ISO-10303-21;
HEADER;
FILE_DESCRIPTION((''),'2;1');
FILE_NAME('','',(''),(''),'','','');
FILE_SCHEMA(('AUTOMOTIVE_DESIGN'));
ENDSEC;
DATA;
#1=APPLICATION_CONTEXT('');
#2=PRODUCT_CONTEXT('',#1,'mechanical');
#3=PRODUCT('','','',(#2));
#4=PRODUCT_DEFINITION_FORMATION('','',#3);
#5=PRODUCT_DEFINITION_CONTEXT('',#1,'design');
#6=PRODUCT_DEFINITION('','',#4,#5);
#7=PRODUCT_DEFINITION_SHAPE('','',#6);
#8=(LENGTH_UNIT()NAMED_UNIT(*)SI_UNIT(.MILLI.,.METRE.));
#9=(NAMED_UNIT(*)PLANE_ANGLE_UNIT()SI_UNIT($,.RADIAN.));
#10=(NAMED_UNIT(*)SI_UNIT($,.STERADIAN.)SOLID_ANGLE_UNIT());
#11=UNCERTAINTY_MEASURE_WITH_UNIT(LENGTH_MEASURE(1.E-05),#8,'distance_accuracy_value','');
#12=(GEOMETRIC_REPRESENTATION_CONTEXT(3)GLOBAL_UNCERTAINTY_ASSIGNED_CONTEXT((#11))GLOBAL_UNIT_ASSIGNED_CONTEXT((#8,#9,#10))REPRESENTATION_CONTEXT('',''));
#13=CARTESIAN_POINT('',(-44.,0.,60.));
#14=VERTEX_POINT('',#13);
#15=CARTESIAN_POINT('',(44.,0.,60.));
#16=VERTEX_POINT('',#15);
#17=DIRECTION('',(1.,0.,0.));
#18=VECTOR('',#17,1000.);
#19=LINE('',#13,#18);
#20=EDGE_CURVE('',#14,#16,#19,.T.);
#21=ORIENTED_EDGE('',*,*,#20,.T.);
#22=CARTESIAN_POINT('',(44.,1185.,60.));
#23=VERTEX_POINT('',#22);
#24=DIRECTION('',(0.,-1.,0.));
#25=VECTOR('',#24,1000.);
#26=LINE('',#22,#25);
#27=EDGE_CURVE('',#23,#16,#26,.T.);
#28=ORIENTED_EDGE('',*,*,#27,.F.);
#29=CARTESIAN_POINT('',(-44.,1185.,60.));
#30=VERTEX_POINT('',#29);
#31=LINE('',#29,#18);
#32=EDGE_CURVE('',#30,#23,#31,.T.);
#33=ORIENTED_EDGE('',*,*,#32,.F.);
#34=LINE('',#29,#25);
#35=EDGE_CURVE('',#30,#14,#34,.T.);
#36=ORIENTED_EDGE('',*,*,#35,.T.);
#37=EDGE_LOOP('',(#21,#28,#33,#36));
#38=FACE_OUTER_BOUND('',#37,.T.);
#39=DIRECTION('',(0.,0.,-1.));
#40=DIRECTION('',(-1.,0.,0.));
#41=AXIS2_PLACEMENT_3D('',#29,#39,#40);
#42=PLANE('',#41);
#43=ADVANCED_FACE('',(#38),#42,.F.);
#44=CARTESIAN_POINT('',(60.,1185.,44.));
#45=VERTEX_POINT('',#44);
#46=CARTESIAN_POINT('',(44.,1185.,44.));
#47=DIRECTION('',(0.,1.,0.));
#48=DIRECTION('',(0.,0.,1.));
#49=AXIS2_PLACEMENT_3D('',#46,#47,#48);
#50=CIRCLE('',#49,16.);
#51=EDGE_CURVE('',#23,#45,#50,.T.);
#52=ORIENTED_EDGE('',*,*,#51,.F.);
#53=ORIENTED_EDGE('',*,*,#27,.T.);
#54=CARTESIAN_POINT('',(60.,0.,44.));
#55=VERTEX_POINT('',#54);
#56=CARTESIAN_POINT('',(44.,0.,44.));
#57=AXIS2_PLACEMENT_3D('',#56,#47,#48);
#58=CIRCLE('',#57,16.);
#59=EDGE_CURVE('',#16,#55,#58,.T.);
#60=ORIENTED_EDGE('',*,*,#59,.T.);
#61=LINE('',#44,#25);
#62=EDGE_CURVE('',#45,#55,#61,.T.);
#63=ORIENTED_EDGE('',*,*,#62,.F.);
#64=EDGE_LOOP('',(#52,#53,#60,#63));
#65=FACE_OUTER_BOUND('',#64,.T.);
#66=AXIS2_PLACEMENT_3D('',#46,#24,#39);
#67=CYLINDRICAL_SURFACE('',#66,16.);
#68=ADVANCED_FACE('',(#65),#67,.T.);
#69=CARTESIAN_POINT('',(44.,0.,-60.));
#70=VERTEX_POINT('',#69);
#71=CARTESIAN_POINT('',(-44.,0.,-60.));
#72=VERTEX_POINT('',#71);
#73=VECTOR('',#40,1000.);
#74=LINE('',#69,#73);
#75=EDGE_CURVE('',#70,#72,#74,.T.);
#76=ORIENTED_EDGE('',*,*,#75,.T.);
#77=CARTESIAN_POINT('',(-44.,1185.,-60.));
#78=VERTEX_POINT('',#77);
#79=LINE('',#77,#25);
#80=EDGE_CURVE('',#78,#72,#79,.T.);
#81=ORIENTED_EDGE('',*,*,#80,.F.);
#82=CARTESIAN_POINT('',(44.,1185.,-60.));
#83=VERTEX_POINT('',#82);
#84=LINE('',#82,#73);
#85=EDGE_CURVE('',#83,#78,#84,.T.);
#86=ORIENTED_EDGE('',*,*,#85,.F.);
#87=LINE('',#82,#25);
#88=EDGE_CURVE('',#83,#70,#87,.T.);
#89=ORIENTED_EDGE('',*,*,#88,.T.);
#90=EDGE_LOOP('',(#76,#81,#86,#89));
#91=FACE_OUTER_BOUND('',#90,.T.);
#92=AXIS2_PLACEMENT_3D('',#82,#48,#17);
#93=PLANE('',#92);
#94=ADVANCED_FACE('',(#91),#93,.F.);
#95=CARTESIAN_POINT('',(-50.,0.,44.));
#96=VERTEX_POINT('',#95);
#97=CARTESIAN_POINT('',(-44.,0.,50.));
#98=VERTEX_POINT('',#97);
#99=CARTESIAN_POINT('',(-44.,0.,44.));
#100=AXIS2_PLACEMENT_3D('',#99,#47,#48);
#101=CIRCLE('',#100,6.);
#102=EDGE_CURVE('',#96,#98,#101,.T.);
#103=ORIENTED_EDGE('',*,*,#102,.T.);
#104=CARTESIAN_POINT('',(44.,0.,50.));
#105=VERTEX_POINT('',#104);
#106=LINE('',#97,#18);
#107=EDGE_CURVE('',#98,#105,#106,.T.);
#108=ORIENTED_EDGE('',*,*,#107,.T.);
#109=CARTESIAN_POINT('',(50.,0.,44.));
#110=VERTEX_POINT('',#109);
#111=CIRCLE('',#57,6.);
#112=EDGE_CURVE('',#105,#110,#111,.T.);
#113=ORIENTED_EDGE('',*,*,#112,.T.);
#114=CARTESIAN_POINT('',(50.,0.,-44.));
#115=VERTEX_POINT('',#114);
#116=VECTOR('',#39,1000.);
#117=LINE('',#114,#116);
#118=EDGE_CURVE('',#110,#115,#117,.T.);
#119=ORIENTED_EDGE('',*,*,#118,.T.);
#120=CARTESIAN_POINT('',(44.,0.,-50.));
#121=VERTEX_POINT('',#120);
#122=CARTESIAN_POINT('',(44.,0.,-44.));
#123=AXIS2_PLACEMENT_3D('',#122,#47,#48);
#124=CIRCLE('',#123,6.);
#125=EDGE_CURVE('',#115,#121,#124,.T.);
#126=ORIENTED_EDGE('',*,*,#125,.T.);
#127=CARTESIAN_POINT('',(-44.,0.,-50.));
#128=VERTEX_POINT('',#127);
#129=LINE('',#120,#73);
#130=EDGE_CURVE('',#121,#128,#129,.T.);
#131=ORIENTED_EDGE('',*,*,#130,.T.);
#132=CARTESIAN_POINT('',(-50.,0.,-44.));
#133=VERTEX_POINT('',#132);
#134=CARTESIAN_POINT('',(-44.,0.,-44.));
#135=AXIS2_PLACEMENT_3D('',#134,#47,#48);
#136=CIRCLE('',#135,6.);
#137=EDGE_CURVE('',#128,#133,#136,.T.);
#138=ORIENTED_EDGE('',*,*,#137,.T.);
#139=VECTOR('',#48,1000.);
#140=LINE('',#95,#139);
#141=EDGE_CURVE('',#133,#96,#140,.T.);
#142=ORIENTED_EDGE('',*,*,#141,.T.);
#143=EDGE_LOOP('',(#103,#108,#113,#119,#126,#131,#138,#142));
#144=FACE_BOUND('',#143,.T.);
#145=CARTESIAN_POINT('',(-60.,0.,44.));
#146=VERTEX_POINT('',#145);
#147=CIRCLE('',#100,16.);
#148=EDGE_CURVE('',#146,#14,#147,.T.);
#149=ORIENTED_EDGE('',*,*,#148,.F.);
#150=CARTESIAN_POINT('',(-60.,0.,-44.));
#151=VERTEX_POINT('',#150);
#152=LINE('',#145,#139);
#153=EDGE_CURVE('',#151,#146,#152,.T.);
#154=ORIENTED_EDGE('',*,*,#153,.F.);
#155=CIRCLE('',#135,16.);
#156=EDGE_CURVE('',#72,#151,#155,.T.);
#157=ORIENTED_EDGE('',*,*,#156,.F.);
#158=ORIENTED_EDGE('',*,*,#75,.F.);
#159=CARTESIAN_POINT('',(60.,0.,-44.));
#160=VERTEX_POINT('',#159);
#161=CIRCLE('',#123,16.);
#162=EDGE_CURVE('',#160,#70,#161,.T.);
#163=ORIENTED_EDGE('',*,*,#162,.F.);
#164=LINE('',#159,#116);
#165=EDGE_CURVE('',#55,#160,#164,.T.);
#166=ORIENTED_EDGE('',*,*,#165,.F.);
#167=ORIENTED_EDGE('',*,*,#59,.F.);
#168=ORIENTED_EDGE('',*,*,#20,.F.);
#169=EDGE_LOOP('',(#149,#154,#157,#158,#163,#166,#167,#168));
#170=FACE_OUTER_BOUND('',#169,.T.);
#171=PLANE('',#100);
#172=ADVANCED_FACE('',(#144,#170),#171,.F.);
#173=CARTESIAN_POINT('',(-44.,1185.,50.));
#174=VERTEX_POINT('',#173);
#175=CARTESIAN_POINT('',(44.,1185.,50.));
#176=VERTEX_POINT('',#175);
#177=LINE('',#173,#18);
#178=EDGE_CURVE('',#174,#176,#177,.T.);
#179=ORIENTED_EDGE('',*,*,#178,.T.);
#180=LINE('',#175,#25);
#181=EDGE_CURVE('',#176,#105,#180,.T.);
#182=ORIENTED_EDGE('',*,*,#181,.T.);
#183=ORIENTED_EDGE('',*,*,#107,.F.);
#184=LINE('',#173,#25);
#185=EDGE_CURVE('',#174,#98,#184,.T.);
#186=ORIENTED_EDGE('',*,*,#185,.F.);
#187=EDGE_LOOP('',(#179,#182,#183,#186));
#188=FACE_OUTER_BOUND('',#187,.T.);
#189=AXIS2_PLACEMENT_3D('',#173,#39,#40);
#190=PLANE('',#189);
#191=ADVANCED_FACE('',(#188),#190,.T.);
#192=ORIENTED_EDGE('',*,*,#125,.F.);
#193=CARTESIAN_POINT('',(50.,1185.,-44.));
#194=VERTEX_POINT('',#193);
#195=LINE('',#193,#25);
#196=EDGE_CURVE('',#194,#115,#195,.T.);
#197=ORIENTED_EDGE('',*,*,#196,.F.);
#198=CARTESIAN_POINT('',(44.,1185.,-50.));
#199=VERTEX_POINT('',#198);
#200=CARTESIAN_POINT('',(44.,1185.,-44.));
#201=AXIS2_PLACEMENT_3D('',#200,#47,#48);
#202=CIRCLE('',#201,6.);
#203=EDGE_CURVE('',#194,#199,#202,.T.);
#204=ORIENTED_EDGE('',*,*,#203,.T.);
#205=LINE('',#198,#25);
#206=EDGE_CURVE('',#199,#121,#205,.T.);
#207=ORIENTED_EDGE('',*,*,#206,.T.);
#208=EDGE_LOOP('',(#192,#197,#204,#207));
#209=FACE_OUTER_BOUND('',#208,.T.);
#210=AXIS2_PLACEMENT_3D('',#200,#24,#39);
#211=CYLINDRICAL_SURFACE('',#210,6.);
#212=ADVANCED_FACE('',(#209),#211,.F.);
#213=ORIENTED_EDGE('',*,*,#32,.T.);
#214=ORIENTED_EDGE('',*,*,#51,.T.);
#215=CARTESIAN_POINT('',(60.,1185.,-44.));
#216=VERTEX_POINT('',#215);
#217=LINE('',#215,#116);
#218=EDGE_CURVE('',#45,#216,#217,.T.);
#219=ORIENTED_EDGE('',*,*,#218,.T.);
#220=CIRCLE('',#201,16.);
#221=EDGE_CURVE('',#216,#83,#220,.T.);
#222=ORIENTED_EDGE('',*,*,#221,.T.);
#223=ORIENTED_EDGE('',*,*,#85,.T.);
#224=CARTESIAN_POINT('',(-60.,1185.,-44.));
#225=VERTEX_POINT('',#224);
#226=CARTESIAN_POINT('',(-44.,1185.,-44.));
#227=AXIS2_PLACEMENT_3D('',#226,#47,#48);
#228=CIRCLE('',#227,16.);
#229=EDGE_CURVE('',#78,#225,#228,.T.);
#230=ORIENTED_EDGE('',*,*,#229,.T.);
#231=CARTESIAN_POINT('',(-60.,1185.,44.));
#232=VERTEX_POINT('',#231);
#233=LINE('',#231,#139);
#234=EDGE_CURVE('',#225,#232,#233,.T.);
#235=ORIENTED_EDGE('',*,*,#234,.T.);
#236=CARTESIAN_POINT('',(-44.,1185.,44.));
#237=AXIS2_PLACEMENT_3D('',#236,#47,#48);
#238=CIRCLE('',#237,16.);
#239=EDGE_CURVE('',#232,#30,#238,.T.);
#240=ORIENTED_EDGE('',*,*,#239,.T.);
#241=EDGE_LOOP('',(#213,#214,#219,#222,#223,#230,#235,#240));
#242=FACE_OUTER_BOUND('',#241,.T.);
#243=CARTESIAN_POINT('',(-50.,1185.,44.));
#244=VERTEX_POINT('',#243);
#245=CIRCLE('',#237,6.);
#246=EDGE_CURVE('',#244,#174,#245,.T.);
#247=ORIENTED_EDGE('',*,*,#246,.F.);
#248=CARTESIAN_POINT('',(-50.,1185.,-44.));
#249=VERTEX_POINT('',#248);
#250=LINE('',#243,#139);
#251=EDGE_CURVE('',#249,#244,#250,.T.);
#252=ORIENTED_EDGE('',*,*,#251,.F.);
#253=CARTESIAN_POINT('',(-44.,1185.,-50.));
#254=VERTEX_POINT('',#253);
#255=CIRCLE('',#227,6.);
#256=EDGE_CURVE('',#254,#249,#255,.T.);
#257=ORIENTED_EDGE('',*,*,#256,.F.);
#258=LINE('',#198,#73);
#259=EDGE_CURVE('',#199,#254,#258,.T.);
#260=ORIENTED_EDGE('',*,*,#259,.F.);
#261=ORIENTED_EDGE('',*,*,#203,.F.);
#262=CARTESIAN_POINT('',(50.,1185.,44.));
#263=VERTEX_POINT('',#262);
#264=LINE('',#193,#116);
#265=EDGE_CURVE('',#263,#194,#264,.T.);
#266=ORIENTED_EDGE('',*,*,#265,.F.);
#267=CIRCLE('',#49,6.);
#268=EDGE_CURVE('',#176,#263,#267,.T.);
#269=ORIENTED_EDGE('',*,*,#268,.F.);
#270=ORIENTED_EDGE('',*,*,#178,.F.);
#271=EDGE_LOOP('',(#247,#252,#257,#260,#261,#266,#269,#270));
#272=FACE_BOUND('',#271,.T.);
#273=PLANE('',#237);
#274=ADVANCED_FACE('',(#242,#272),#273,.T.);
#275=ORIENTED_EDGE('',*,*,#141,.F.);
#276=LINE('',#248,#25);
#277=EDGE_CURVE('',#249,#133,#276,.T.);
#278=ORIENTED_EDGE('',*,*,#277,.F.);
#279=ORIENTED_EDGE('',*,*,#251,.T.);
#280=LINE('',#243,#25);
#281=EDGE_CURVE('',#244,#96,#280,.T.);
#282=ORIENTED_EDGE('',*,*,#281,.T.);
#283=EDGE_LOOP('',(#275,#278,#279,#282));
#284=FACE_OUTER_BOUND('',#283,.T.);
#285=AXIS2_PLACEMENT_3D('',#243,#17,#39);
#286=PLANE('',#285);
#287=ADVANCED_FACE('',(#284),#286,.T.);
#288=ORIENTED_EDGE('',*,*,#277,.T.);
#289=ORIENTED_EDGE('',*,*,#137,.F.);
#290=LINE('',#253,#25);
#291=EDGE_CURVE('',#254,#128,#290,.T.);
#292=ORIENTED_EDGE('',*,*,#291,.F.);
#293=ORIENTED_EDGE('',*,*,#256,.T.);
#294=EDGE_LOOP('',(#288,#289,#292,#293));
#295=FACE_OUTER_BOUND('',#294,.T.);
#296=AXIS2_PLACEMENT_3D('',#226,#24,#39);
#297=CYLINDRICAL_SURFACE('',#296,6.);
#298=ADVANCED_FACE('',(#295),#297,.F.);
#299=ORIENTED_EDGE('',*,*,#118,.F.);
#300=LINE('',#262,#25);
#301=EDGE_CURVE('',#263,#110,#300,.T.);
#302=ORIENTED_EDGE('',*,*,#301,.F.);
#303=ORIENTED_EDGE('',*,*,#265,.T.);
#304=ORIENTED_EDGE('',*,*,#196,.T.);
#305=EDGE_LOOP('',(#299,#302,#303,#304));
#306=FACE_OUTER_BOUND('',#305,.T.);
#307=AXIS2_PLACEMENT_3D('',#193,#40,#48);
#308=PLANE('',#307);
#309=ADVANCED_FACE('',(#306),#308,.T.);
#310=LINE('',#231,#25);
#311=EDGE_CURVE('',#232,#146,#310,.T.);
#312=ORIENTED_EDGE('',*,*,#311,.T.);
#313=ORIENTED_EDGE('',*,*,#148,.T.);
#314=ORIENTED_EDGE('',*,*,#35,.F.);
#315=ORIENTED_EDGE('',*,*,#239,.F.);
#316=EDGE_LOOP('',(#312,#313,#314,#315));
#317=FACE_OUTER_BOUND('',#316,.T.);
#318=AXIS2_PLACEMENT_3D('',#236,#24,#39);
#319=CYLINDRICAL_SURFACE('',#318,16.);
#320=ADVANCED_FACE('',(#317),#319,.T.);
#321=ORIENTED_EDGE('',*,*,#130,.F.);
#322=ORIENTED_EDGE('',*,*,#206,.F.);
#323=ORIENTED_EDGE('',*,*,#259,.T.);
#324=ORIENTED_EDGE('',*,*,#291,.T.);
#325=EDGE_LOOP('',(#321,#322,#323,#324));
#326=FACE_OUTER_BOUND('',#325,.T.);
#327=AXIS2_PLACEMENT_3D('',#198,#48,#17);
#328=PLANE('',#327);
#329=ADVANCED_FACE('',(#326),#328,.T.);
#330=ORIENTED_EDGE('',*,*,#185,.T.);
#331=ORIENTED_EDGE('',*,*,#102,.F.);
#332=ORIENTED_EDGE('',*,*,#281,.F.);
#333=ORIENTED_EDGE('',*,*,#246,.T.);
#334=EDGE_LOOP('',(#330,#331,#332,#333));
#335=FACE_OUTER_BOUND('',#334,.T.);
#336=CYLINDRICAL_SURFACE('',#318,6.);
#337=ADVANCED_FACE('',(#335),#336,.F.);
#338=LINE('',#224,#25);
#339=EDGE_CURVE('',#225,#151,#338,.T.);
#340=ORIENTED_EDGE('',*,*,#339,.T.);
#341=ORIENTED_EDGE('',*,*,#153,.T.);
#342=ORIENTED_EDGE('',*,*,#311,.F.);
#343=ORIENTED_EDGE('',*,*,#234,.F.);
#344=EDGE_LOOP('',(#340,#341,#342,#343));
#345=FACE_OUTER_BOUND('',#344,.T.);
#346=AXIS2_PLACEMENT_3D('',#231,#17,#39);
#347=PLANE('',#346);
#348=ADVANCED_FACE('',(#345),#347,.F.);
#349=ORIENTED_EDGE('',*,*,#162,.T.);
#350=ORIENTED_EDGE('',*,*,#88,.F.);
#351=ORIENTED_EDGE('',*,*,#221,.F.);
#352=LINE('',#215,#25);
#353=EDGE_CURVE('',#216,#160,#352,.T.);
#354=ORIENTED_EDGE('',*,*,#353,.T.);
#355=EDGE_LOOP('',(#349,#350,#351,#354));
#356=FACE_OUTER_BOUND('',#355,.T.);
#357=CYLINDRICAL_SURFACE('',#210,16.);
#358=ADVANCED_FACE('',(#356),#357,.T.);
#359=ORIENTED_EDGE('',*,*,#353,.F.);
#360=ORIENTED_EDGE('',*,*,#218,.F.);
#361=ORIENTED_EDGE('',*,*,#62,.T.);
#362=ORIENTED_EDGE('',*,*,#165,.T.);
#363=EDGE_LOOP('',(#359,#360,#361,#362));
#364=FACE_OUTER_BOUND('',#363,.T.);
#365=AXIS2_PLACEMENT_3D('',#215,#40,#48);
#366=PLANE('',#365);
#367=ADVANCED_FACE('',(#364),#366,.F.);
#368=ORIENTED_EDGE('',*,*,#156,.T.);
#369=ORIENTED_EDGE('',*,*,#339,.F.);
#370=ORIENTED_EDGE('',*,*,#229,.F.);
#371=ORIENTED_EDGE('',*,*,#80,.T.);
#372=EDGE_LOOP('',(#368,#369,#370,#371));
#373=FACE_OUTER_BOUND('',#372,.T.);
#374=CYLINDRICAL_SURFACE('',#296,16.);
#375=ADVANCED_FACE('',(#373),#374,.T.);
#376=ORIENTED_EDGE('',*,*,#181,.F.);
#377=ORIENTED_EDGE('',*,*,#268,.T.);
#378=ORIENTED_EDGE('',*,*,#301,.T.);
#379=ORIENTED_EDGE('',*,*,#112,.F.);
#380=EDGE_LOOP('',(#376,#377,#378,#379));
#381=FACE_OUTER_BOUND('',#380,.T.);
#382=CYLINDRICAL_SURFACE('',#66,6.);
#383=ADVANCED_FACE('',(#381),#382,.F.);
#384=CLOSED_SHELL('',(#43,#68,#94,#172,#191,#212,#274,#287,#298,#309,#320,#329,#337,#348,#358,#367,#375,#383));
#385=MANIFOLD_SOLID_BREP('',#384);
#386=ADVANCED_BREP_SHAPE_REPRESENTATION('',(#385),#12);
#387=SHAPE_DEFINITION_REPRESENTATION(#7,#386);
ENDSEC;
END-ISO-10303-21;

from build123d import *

# Parameters (mm, degrees)
GB_T6728_2002_120_120_10_1_DEPTH = 1185


with BuildPart() as part:
    # Sketch12 → 结构用冷弯空心方钢(gb t6728-2002) 120×120×10(1) (new body)
    with BuildSketch(Plane(origin=(0, 0, 0), x_dir=(-1, 0, 0), z_dir=(0, 1, 0))):
        with BuildLine():
            Line((-44, -60), (44, -60))
            ThreePointArc((44, -60), (55.313708499, -55.313708499), (60, -44))
            Line((60, -44), (60, 44))
            ThreePointArc((60, 44), (55.313708499, 55.313708499), (44, 60))
            Line((44, 60), (-44, 60))
            ThreePointArc((-44, 60), (-55.313708499, 55.313708499), (-60, 44))
            Line((-60, 44), (-60, -44))
            ThreePointArc((-60, -44), (-55.313708499, -55.313708499), (-44, -60))
        make_face()
        with BuildLine():
            Line((-44, -50), (44, -50))
            ThreePointArc((44, -50), (48.242640687, -48.242640687), (50, -44))
            Line((50, -44), (50, 44))
            ThreePointArc((50, 44), (48.242640687, 48.242640687), (44, 50))
            Line((44, 50), (-44, 50))
            ThreePointArc((-44, 50), (-48.242640687, 48.242640687), (-50, 44))
            Line((-50, 44), (-50, -44))
            ThreePointArc((-50, -44), (-48.242640687, -48.242640687), (-44, -50))
        make_face(mode=Mode.SUBTRACT)
    extrude(amount=GB_T6728_2002_120_120_10_1_DEPTH)


solid = part.part
